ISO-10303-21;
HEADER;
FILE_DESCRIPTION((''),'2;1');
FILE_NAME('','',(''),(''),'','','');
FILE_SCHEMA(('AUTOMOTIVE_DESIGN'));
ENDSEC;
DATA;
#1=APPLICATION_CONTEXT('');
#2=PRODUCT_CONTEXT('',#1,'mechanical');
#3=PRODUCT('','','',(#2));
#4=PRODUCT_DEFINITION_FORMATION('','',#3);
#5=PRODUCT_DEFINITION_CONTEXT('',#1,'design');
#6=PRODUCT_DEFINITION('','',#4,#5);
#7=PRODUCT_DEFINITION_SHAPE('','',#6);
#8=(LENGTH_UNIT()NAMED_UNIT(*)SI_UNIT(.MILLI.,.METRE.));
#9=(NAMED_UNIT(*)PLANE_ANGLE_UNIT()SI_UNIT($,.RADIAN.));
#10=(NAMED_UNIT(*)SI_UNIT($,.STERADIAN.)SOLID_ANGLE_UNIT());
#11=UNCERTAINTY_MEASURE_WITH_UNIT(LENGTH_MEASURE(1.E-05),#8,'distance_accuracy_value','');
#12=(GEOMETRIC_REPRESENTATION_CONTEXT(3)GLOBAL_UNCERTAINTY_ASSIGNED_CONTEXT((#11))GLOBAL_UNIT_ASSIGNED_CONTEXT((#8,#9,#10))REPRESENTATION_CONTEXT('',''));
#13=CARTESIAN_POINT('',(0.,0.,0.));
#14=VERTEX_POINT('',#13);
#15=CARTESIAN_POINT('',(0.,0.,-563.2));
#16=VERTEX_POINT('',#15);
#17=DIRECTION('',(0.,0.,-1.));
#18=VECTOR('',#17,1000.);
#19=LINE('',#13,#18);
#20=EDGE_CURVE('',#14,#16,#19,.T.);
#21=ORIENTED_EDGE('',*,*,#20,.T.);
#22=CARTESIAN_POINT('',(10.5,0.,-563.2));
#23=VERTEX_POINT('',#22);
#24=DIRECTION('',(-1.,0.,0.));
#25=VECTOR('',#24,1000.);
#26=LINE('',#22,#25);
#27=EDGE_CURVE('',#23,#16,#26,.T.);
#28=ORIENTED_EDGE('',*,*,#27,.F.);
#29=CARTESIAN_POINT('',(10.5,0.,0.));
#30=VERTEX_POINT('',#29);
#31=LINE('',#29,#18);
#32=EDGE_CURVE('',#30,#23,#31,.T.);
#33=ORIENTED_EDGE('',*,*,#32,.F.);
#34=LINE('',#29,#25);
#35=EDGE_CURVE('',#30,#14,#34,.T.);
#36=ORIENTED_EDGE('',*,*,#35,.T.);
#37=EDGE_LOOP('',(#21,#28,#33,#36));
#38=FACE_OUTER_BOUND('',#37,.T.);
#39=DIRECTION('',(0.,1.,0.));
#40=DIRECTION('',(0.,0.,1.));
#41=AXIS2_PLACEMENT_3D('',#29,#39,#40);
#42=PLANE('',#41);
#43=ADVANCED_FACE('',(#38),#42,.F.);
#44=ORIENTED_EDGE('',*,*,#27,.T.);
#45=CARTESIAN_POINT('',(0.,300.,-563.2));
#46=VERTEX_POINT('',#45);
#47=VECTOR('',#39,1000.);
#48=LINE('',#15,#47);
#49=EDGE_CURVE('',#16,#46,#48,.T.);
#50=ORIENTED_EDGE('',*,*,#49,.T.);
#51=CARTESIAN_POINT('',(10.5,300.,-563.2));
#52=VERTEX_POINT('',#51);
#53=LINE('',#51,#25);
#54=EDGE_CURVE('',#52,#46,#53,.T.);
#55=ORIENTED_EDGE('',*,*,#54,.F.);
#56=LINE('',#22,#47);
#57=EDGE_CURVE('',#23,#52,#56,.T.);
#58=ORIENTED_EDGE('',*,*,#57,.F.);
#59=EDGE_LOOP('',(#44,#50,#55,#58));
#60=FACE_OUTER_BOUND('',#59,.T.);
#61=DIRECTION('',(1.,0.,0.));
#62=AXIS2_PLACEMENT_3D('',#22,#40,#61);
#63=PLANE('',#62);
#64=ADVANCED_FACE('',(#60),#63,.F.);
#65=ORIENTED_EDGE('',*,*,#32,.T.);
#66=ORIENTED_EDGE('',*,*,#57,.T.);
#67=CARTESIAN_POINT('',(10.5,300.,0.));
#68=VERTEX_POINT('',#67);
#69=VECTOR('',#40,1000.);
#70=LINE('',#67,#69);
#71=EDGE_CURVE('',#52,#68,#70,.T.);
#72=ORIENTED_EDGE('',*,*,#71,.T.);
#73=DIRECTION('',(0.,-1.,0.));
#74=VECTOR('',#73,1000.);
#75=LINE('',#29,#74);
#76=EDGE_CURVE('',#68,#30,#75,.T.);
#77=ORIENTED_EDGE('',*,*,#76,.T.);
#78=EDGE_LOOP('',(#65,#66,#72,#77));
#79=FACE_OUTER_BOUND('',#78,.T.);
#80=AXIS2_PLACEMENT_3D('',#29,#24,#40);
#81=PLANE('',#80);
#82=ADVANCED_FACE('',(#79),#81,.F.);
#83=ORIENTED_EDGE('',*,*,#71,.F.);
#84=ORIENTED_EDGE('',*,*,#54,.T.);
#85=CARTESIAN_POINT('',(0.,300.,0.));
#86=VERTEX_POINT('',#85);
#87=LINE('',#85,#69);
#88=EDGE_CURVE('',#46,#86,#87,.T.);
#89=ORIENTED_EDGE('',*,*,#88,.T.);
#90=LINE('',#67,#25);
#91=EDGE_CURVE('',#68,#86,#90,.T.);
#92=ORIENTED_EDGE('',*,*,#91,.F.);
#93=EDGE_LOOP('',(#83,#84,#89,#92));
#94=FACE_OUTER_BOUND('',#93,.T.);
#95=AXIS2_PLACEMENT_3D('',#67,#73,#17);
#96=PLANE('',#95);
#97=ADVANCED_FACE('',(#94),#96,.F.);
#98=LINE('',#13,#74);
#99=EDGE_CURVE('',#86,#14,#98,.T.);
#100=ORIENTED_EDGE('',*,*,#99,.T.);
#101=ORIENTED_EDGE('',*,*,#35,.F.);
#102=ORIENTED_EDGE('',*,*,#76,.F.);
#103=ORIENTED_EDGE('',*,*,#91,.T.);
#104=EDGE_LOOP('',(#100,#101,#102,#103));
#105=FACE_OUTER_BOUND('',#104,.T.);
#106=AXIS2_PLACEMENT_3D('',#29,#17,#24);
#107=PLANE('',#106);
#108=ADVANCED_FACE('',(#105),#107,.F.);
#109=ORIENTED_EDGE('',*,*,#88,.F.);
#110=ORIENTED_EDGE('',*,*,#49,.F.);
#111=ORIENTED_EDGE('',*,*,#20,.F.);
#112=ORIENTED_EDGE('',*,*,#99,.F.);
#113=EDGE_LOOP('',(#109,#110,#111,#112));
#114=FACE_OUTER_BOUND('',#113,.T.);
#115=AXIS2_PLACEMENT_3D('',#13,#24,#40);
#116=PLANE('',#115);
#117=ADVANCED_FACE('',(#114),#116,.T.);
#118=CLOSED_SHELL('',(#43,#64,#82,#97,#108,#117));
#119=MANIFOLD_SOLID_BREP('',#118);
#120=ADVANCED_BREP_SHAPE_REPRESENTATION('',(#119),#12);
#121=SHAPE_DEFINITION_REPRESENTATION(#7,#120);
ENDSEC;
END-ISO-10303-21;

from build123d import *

# Parameters (mm, degrees)
SKETCH1_W           = 563.2
SKETCH1_H           = 300
BOSS_EXTRUDE1_DEPTH = 10.5


with BuildPart() as part:
    # Sketch1 → Boss-Extrude1 (new body)
    with BuildSketch(Plane(origin=(0, 0, 0), x_dir=(0, 0, -1), z_dir=(1, 0, 0))):
        with Locations((281.6, 150)):
            Rectangle(SKETCH1_W, SKETCH1_H)
    extrude(amount=BOSS_EXTRUDE1_DEPTH)


solid = part.part
